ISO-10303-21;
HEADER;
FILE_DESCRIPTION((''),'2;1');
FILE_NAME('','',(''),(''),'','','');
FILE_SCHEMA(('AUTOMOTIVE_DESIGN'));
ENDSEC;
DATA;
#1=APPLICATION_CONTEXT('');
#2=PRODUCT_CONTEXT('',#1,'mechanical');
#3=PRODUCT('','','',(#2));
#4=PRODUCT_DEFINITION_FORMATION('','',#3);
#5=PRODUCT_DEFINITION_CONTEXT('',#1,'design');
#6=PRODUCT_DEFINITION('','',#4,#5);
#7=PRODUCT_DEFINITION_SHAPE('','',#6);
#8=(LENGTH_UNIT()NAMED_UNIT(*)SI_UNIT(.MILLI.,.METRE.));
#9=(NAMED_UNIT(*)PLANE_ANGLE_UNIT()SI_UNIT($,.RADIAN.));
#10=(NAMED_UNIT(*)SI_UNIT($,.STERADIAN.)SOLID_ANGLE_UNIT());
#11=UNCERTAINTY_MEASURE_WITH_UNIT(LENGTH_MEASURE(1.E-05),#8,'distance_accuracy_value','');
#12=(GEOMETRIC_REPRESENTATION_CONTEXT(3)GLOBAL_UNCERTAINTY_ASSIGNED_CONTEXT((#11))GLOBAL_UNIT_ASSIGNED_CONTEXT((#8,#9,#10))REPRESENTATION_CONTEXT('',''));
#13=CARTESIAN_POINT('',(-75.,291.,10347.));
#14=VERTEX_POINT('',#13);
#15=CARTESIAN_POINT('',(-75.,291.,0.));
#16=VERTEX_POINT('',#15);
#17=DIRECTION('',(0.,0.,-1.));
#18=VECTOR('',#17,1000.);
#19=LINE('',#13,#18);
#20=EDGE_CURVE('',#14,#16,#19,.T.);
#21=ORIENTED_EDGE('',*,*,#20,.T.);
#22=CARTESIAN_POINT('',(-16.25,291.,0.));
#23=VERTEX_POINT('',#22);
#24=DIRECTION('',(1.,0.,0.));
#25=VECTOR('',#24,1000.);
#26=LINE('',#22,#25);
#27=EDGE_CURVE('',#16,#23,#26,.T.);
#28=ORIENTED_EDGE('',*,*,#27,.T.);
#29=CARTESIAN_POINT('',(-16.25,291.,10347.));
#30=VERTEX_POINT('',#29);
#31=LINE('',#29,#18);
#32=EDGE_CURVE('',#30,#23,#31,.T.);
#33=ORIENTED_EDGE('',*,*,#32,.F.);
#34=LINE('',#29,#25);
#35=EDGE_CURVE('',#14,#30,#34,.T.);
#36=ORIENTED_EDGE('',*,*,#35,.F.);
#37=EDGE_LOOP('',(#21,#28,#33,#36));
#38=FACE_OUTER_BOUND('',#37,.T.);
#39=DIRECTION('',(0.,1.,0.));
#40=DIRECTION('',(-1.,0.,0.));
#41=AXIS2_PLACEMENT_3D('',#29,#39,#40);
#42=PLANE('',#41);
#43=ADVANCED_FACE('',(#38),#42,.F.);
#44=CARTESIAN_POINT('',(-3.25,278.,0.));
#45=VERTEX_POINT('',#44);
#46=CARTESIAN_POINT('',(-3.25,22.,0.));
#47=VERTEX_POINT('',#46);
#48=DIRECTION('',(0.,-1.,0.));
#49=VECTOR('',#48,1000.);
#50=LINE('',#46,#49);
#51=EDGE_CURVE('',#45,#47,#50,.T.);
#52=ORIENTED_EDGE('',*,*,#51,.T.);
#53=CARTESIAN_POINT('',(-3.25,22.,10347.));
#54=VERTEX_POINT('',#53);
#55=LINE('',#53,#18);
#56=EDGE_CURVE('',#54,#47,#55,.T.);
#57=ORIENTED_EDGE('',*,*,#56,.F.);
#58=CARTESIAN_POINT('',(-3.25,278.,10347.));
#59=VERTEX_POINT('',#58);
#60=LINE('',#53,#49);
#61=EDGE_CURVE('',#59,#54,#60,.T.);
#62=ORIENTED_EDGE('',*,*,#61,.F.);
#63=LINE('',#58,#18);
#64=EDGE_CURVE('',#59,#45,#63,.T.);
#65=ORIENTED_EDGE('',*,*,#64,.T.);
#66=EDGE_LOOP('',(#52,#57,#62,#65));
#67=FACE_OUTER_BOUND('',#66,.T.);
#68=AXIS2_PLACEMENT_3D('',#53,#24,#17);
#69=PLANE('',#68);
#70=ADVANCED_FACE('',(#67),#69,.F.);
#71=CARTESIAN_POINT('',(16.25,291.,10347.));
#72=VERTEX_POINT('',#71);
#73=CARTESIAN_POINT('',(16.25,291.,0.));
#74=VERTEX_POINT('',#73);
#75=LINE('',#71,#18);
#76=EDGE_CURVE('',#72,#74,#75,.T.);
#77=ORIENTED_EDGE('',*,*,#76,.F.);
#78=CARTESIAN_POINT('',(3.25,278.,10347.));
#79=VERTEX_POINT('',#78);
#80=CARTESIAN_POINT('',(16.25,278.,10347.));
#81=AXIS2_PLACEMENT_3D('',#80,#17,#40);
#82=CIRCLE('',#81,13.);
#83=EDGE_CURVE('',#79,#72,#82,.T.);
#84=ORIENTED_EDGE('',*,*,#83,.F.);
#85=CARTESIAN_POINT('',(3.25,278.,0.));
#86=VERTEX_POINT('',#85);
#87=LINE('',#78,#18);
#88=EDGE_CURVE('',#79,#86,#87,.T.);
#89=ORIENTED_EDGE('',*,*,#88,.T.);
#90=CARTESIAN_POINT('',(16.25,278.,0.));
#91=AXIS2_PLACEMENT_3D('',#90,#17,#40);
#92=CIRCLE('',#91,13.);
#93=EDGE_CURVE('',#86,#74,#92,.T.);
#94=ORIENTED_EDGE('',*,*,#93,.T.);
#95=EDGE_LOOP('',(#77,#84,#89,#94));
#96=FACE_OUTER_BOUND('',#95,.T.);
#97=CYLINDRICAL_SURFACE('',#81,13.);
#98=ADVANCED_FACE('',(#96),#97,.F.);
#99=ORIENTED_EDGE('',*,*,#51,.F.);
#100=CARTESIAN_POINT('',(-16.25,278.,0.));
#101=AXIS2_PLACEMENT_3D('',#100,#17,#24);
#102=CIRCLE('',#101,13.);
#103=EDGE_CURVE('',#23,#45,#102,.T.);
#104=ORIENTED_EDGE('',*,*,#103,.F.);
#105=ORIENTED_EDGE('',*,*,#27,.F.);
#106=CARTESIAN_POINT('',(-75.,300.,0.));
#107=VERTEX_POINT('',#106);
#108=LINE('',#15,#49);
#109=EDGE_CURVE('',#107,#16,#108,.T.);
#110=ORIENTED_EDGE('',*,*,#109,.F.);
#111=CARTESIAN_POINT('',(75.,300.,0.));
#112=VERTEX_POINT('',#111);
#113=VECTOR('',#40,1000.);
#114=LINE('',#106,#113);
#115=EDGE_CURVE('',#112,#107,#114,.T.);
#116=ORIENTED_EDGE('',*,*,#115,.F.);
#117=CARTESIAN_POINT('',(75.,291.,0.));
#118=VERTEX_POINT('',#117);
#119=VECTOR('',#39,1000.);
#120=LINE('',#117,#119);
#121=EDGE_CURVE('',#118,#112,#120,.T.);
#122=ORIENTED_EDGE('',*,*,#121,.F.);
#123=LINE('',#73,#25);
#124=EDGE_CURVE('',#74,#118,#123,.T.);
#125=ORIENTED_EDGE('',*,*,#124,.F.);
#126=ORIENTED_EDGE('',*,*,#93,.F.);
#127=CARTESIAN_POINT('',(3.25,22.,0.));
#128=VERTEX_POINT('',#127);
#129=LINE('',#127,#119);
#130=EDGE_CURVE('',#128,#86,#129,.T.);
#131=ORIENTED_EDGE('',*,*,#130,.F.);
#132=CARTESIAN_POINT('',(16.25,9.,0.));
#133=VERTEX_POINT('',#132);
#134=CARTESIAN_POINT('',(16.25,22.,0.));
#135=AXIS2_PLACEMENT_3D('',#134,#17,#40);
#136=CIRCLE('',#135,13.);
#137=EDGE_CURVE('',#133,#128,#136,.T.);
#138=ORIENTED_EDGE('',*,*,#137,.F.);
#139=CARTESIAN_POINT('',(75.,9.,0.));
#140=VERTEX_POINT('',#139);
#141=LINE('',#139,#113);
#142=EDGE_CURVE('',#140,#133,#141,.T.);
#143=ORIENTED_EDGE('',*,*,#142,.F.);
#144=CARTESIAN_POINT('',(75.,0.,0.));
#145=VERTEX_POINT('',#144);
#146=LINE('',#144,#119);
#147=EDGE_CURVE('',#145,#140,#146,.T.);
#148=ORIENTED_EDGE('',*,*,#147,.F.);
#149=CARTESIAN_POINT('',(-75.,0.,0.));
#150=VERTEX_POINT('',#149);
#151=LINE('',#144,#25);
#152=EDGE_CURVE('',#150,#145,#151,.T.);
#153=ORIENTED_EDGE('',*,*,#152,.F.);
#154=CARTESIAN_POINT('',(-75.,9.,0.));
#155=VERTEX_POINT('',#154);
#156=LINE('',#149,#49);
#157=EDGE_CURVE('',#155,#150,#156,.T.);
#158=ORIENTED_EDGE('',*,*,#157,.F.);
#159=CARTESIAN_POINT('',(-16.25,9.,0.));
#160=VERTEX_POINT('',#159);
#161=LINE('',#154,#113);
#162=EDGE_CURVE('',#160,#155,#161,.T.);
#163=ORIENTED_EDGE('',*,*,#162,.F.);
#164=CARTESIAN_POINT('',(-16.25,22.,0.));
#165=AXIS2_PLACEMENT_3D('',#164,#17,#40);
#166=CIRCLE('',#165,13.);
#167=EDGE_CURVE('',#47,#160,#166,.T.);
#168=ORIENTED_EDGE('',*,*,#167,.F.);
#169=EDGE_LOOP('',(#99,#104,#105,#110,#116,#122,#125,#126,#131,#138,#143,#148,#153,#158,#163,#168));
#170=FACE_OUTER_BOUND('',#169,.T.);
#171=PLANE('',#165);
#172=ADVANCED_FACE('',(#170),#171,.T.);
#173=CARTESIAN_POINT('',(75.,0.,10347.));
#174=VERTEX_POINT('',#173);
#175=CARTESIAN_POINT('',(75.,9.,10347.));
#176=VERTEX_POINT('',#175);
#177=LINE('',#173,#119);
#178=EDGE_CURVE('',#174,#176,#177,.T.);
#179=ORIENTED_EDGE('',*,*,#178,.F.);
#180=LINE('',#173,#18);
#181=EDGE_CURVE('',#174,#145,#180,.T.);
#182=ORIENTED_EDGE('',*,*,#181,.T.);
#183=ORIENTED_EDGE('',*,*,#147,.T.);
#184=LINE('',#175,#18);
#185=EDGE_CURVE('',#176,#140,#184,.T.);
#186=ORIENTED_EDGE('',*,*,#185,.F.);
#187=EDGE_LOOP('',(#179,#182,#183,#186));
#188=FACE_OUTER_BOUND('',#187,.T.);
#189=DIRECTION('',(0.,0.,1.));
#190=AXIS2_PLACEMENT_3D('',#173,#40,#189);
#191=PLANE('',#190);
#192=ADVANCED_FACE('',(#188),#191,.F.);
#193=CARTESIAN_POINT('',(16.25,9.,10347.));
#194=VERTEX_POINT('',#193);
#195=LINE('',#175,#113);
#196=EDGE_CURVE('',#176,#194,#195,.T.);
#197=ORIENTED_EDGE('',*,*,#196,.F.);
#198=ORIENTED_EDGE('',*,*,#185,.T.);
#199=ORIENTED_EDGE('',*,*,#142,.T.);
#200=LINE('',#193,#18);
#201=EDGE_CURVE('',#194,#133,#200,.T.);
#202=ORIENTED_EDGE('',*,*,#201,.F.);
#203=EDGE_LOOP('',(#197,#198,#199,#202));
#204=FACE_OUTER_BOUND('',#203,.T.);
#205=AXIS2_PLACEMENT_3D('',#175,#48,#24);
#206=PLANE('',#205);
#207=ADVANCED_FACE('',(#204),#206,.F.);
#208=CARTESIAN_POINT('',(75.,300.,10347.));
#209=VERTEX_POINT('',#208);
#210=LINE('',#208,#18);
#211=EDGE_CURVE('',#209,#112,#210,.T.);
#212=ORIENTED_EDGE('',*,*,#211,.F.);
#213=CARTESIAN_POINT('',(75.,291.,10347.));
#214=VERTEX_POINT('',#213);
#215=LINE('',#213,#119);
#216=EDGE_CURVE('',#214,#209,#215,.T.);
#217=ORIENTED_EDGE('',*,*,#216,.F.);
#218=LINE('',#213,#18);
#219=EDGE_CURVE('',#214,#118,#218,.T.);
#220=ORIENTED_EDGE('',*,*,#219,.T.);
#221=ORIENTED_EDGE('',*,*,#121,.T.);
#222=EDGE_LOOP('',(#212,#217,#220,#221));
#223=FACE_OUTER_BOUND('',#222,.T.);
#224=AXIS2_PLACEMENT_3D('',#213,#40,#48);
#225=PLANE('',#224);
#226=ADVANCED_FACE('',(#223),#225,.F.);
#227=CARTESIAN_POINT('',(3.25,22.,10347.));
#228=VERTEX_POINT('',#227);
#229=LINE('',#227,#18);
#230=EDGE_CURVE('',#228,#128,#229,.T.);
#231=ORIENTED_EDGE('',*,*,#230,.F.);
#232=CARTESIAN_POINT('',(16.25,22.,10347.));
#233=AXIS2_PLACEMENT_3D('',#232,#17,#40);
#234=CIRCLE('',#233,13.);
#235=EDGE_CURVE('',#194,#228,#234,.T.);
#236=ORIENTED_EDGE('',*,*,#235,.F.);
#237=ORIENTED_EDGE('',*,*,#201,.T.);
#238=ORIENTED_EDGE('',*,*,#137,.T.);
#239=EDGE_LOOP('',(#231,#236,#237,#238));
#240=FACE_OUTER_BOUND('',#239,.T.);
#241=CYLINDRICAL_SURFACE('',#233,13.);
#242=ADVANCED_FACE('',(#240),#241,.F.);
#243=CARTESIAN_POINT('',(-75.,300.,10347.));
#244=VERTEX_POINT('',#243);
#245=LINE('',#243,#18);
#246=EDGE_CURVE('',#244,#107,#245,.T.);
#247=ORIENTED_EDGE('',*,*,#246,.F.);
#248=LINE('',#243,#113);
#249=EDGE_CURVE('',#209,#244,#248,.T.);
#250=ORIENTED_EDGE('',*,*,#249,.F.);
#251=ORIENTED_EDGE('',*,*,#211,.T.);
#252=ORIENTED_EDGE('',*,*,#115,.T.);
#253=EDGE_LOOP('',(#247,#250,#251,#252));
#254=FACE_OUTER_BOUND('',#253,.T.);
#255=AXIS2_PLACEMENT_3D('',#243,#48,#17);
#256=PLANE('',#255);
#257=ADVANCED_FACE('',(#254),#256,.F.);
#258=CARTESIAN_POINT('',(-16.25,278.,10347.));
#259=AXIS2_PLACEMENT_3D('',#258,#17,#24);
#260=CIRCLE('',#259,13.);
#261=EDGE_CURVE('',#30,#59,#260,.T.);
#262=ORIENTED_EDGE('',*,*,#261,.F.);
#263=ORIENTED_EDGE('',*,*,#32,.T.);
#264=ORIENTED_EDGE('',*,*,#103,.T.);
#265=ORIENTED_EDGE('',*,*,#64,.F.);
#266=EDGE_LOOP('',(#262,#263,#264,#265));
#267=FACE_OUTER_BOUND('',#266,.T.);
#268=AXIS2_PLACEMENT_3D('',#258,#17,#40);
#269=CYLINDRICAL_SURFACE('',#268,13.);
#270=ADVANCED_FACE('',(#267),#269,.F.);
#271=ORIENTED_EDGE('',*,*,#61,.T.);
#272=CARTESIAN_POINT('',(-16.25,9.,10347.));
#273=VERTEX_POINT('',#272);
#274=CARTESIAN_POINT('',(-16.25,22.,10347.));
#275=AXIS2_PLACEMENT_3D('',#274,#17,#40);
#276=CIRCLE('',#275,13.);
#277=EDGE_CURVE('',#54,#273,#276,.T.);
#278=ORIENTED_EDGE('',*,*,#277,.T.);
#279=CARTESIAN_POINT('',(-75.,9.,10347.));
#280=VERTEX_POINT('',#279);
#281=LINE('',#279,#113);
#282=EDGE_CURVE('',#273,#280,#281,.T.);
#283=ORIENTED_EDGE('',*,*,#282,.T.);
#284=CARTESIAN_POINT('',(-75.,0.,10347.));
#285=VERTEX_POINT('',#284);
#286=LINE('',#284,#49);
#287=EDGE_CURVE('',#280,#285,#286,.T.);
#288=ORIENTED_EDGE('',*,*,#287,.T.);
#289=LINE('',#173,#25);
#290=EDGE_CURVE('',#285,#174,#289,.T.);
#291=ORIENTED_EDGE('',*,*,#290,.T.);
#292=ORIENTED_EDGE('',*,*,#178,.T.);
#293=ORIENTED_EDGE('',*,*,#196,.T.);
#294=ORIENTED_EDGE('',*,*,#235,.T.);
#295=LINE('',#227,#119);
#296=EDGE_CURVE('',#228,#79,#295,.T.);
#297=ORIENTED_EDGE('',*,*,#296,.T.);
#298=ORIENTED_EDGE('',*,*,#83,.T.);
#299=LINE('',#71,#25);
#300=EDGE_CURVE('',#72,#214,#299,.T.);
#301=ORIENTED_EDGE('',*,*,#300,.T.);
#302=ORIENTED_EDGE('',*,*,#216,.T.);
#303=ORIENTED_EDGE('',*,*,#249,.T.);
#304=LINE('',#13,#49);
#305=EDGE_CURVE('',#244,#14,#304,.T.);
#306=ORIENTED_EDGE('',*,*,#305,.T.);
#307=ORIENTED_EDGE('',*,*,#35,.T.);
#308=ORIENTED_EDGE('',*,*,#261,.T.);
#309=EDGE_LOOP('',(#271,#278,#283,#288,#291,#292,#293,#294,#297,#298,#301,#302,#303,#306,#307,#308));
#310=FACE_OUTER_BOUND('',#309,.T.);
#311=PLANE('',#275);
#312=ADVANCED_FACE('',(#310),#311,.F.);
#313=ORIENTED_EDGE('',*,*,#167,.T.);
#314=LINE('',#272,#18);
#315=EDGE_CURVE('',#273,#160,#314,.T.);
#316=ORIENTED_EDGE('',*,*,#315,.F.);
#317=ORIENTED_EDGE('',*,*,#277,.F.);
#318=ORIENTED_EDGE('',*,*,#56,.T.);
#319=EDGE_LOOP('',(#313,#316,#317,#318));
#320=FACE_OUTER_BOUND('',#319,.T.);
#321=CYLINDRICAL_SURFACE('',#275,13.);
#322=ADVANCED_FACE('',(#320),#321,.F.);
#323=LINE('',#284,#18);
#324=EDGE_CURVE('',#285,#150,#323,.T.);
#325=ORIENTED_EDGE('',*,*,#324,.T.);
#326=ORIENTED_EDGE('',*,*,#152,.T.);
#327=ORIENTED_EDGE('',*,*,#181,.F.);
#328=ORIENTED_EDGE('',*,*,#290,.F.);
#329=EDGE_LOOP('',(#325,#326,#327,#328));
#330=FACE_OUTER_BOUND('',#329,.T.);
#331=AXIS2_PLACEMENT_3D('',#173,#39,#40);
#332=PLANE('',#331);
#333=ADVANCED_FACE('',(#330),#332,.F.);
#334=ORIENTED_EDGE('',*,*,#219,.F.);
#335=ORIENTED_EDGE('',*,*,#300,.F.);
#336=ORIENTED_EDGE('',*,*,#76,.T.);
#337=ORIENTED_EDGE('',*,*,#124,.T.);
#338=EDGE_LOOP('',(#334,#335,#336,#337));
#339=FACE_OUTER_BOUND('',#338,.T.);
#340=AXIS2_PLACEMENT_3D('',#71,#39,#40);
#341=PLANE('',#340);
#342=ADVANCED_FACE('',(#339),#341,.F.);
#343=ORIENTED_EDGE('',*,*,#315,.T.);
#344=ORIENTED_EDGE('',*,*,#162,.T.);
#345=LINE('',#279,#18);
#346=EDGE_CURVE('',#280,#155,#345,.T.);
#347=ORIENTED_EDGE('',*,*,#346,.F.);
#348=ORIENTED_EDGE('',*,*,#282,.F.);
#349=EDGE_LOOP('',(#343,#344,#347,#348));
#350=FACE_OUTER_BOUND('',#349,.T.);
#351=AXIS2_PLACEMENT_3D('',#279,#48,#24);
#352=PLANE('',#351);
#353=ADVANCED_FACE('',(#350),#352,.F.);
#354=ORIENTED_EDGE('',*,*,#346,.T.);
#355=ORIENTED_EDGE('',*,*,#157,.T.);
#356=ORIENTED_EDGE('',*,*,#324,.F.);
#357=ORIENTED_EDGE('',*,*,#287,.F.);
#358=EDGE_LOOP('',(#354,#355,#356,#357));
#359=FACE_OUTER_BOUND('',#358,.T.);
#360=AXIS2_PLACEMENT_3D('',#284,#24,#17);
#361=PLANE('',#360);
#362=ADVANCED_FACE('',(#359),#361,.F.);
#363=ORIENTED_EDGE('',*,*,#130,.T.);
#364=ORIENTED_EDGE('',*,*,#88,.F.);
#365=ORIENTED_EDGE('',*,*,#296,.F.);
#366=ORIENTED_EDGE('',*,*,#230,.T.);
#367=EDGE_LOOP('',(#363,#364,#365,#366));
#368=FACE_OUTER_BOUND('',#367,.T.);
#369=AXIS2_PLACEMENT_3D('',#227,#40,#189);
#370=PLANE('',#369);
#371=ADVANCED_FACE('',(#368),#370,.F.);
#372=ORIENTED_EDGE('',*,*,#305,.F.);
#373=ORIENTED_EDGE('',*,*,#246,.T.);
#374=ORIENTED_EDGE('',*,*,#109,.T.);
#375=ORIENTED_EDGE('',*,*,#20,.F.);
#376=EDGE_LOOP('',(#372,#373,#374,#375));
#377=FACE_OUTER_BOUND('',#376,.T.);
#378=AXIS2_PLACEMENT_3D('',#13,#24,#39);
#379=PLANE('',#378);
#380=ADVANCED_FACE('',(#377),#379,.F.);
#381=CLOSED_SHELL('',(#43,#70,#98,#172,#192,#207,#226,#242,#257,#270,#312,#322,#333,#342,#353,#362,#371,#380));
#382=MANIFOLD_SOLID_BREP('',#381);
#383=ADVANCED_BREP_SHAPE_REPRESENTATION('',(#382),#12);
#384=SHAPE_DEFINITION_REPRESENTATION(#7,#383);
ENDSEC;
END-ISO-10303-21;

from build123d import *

# Parameters (mm, degrees)
BOSS_EXTRUDE1_DEPTH = 10347


with BuildPart() as part:
    # Sketch1 → Boss-Extrude1 (new body)
    with BuildSketch(Plane.XY):
        with BuildLine():
            Line((75, 0), (-75, 0))
            Line((-75, 0), (-75, 9))
            Line((-75, 9), (-16.25, 9))
            ThreePointArc((-16.25, 9), (-7.057611845, 12.807611845), (-3.25, 22))
            Line((-3.25, 22), (-3.25, 278))
            ThreePointArc((-3.25, 278), (-7.057611845, 287.192388155), (-16.25, 291))
            Line((-16.25, 291), (-75, 291))
            Line((-75, 291), (-75, 300))
            Line((-75, 300), (75, 300))
            Line((75, 300), (75, 291))
            Line((75, 291), (16.25, 291))
            ThreePointArc((16.25, 291), (7.057611845, 287.192388155), (3.25, 278))
            Line((3.25, 278), (3.25, 22))
            ThreePointArc((3.25, 22), (7.057611845, 12.807611845), (16.25, 9))
            Line((16.25, 9), (75, 9))
            Line((75, 9), (75, 0))
        make_face()
    extrude(amount=BOSS_EXTRUDE1_DEPTH)


solid = part.part
